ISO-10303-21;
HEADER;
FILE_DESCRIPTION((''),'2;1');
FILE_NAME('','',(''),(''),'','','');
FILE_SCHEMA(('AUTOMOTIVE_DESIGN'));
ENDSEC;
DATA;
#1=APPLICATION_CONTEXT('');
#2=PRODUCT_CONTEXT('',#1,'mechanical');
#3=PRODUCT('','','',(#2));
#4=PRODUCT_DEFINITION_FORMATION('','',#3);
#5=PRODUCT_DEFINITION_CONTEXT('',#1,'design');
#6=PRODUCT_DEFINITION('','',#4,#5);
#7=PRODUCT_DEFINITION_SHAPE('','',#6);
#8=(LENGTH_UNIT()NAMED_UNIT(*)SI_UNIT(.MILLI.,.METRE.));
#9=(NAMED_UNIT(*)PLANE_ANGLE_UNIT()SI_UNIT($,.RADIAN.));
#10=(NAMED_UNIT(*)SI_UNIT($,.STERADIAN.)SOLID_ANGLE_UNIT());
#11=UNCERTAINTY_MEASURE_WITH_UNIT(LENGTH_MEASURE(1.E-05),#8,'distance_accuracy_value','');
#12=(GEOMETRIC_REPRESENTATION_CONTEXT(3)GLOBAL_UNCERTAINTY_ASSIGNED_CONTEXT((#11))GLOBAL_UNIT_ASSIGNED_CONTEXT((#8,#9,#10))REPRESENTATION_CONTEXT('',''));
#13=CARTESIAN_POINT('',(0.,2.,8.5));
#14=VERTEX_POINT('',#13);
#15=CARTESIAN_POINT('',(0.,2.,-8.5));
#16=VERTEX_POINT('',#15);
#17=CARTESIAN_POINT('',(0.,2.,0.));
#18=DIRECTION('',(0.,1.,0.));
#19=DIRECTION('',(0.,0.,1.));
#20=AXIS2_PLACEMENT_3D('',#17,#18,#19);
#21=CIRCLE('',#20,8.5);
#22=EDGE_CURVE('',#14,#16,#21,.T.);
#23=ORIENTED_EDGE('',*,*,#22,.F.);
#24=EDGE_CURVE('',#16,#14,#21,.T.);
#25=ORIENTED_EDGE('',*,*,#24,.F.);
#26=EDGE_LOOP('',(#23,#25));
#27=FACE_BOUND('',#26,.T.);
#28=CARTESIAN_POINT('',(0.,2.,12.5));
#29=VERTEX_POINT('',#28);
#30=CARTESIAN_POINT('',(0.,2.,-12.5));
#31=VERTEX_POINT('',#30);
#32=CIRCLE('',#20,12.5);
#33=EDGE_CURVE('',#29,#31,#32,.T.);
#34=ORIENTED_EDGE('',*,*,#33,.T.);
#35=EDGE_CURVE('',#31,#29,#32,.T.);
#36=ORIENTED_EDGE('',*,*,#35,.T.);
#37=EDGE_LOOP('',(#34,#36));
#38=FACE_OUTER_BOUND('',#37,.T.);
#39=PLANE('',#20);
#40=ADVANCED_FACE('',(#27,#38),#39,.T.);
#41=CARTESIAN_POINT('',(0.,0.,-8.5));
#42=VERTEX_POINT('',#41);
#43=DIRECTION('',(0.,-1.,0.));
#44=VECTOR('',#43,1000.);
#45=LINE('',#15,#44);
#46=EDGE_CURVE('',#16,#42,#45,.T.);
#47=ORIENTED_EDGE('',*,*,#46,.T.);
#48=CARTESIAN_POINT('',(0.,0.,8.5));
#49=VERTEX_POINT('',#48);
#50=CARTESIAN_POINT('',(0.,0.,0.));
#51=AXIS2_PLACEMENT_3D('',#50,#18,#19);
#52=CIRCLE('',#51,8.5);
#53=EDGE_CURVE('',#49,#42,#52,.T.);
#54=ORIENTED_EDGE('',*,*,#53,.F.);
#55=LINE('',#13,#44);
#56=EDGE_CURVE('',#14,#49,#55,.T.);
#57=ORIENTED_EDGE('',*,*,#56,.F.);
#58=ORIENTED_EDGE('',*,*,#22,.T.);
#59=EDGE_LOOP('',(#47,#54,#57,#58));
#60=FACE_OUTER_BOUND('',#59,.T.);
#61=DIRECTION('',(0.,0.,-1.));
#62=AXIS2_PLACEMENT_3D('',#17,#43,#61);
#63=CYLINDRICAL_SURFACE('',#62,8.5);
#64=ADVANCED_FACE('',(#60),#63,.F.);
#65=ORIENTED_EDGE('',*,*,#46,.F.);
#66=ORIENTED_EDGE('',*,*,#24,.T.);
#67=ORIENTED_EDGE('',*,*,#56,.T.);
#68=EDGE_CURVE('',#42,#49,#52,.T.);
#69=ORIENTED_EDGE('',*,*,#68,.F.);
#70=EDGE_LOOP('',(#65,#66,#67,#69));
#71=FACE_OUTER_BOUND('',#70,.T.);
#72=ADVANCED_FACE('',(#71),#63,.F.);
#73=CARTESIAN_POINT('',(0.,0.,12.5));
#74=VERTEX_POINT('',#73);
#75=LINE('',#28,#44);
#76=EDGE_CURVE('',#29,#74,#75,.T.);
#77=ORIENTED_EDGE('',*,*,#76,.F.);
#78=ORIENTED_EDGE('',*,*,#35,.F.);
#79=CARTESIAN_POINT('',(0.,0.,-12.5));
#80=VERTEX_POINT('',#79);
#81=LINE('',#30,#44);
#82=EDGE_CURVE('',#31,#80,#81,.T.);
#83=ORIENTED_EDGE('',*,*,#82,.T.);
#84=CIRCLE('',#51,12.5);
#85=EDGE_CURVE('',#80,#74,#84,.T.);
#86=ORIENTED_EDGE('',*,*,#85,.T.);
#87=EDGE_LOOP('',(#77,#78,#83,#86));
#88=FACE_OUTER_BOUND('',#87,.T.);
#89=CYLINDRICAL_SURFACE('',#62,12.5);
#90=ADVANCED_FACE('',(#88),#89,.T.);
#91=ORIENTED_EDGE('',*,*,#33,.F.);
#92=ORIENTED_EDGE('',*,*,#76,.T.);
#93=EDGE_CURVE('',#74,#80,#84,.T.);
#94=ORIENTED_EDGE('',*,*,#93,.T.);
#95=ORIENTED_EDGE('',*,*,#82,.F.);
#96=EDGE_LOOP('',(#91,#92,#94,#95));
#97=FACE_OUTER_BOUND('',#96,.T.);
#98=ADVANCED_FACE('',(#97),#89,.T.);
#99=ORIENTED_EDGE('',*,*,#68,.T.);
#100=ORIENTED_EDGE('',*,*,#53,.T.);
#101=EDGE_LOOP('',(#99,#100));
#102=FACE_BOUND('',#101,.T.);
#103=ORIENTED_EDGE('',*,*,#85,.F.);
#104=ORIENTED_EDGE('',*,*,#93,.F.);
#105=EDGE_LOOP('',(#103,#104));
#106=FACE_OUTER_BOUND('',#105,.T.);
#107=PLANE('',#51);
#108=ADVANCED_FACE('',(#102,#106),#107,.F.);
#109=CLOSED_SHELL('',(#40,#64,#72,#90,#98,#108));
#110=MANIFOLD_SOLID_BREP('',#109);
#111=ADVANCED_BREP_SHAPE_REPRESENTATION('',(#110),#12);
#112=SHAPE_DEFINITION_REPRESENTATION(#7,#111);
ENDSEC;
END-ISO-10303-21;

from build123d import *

# Parameters (mm, degrees)
SKETCH1_R           = 12.5
SKETCH1_R_2         = 8.5
BOSS_EXTRUDE1_DEPTH = 2


with BuildPart() as part:
    # Sketch1 → Boss-Extrude1 (new body)
    with BuildSketch(Plane(origin=(0, 0, 0), x_dir=(1, 0, 0), z_dir=(0, 1, 0))):
        with Locations(Location((0, 0, 0), (0, 0, 270))):
            Circle(SKETCH1_R)
        with Locations(Location((0, 0, 0), (0, 0, 270))):
            Circle(SKETCH1_R_2, mode=Mode.SUBTRACT)
    extrude(amount=BOSS_EXTRUDE1_DEPTH)


solid = part.part
